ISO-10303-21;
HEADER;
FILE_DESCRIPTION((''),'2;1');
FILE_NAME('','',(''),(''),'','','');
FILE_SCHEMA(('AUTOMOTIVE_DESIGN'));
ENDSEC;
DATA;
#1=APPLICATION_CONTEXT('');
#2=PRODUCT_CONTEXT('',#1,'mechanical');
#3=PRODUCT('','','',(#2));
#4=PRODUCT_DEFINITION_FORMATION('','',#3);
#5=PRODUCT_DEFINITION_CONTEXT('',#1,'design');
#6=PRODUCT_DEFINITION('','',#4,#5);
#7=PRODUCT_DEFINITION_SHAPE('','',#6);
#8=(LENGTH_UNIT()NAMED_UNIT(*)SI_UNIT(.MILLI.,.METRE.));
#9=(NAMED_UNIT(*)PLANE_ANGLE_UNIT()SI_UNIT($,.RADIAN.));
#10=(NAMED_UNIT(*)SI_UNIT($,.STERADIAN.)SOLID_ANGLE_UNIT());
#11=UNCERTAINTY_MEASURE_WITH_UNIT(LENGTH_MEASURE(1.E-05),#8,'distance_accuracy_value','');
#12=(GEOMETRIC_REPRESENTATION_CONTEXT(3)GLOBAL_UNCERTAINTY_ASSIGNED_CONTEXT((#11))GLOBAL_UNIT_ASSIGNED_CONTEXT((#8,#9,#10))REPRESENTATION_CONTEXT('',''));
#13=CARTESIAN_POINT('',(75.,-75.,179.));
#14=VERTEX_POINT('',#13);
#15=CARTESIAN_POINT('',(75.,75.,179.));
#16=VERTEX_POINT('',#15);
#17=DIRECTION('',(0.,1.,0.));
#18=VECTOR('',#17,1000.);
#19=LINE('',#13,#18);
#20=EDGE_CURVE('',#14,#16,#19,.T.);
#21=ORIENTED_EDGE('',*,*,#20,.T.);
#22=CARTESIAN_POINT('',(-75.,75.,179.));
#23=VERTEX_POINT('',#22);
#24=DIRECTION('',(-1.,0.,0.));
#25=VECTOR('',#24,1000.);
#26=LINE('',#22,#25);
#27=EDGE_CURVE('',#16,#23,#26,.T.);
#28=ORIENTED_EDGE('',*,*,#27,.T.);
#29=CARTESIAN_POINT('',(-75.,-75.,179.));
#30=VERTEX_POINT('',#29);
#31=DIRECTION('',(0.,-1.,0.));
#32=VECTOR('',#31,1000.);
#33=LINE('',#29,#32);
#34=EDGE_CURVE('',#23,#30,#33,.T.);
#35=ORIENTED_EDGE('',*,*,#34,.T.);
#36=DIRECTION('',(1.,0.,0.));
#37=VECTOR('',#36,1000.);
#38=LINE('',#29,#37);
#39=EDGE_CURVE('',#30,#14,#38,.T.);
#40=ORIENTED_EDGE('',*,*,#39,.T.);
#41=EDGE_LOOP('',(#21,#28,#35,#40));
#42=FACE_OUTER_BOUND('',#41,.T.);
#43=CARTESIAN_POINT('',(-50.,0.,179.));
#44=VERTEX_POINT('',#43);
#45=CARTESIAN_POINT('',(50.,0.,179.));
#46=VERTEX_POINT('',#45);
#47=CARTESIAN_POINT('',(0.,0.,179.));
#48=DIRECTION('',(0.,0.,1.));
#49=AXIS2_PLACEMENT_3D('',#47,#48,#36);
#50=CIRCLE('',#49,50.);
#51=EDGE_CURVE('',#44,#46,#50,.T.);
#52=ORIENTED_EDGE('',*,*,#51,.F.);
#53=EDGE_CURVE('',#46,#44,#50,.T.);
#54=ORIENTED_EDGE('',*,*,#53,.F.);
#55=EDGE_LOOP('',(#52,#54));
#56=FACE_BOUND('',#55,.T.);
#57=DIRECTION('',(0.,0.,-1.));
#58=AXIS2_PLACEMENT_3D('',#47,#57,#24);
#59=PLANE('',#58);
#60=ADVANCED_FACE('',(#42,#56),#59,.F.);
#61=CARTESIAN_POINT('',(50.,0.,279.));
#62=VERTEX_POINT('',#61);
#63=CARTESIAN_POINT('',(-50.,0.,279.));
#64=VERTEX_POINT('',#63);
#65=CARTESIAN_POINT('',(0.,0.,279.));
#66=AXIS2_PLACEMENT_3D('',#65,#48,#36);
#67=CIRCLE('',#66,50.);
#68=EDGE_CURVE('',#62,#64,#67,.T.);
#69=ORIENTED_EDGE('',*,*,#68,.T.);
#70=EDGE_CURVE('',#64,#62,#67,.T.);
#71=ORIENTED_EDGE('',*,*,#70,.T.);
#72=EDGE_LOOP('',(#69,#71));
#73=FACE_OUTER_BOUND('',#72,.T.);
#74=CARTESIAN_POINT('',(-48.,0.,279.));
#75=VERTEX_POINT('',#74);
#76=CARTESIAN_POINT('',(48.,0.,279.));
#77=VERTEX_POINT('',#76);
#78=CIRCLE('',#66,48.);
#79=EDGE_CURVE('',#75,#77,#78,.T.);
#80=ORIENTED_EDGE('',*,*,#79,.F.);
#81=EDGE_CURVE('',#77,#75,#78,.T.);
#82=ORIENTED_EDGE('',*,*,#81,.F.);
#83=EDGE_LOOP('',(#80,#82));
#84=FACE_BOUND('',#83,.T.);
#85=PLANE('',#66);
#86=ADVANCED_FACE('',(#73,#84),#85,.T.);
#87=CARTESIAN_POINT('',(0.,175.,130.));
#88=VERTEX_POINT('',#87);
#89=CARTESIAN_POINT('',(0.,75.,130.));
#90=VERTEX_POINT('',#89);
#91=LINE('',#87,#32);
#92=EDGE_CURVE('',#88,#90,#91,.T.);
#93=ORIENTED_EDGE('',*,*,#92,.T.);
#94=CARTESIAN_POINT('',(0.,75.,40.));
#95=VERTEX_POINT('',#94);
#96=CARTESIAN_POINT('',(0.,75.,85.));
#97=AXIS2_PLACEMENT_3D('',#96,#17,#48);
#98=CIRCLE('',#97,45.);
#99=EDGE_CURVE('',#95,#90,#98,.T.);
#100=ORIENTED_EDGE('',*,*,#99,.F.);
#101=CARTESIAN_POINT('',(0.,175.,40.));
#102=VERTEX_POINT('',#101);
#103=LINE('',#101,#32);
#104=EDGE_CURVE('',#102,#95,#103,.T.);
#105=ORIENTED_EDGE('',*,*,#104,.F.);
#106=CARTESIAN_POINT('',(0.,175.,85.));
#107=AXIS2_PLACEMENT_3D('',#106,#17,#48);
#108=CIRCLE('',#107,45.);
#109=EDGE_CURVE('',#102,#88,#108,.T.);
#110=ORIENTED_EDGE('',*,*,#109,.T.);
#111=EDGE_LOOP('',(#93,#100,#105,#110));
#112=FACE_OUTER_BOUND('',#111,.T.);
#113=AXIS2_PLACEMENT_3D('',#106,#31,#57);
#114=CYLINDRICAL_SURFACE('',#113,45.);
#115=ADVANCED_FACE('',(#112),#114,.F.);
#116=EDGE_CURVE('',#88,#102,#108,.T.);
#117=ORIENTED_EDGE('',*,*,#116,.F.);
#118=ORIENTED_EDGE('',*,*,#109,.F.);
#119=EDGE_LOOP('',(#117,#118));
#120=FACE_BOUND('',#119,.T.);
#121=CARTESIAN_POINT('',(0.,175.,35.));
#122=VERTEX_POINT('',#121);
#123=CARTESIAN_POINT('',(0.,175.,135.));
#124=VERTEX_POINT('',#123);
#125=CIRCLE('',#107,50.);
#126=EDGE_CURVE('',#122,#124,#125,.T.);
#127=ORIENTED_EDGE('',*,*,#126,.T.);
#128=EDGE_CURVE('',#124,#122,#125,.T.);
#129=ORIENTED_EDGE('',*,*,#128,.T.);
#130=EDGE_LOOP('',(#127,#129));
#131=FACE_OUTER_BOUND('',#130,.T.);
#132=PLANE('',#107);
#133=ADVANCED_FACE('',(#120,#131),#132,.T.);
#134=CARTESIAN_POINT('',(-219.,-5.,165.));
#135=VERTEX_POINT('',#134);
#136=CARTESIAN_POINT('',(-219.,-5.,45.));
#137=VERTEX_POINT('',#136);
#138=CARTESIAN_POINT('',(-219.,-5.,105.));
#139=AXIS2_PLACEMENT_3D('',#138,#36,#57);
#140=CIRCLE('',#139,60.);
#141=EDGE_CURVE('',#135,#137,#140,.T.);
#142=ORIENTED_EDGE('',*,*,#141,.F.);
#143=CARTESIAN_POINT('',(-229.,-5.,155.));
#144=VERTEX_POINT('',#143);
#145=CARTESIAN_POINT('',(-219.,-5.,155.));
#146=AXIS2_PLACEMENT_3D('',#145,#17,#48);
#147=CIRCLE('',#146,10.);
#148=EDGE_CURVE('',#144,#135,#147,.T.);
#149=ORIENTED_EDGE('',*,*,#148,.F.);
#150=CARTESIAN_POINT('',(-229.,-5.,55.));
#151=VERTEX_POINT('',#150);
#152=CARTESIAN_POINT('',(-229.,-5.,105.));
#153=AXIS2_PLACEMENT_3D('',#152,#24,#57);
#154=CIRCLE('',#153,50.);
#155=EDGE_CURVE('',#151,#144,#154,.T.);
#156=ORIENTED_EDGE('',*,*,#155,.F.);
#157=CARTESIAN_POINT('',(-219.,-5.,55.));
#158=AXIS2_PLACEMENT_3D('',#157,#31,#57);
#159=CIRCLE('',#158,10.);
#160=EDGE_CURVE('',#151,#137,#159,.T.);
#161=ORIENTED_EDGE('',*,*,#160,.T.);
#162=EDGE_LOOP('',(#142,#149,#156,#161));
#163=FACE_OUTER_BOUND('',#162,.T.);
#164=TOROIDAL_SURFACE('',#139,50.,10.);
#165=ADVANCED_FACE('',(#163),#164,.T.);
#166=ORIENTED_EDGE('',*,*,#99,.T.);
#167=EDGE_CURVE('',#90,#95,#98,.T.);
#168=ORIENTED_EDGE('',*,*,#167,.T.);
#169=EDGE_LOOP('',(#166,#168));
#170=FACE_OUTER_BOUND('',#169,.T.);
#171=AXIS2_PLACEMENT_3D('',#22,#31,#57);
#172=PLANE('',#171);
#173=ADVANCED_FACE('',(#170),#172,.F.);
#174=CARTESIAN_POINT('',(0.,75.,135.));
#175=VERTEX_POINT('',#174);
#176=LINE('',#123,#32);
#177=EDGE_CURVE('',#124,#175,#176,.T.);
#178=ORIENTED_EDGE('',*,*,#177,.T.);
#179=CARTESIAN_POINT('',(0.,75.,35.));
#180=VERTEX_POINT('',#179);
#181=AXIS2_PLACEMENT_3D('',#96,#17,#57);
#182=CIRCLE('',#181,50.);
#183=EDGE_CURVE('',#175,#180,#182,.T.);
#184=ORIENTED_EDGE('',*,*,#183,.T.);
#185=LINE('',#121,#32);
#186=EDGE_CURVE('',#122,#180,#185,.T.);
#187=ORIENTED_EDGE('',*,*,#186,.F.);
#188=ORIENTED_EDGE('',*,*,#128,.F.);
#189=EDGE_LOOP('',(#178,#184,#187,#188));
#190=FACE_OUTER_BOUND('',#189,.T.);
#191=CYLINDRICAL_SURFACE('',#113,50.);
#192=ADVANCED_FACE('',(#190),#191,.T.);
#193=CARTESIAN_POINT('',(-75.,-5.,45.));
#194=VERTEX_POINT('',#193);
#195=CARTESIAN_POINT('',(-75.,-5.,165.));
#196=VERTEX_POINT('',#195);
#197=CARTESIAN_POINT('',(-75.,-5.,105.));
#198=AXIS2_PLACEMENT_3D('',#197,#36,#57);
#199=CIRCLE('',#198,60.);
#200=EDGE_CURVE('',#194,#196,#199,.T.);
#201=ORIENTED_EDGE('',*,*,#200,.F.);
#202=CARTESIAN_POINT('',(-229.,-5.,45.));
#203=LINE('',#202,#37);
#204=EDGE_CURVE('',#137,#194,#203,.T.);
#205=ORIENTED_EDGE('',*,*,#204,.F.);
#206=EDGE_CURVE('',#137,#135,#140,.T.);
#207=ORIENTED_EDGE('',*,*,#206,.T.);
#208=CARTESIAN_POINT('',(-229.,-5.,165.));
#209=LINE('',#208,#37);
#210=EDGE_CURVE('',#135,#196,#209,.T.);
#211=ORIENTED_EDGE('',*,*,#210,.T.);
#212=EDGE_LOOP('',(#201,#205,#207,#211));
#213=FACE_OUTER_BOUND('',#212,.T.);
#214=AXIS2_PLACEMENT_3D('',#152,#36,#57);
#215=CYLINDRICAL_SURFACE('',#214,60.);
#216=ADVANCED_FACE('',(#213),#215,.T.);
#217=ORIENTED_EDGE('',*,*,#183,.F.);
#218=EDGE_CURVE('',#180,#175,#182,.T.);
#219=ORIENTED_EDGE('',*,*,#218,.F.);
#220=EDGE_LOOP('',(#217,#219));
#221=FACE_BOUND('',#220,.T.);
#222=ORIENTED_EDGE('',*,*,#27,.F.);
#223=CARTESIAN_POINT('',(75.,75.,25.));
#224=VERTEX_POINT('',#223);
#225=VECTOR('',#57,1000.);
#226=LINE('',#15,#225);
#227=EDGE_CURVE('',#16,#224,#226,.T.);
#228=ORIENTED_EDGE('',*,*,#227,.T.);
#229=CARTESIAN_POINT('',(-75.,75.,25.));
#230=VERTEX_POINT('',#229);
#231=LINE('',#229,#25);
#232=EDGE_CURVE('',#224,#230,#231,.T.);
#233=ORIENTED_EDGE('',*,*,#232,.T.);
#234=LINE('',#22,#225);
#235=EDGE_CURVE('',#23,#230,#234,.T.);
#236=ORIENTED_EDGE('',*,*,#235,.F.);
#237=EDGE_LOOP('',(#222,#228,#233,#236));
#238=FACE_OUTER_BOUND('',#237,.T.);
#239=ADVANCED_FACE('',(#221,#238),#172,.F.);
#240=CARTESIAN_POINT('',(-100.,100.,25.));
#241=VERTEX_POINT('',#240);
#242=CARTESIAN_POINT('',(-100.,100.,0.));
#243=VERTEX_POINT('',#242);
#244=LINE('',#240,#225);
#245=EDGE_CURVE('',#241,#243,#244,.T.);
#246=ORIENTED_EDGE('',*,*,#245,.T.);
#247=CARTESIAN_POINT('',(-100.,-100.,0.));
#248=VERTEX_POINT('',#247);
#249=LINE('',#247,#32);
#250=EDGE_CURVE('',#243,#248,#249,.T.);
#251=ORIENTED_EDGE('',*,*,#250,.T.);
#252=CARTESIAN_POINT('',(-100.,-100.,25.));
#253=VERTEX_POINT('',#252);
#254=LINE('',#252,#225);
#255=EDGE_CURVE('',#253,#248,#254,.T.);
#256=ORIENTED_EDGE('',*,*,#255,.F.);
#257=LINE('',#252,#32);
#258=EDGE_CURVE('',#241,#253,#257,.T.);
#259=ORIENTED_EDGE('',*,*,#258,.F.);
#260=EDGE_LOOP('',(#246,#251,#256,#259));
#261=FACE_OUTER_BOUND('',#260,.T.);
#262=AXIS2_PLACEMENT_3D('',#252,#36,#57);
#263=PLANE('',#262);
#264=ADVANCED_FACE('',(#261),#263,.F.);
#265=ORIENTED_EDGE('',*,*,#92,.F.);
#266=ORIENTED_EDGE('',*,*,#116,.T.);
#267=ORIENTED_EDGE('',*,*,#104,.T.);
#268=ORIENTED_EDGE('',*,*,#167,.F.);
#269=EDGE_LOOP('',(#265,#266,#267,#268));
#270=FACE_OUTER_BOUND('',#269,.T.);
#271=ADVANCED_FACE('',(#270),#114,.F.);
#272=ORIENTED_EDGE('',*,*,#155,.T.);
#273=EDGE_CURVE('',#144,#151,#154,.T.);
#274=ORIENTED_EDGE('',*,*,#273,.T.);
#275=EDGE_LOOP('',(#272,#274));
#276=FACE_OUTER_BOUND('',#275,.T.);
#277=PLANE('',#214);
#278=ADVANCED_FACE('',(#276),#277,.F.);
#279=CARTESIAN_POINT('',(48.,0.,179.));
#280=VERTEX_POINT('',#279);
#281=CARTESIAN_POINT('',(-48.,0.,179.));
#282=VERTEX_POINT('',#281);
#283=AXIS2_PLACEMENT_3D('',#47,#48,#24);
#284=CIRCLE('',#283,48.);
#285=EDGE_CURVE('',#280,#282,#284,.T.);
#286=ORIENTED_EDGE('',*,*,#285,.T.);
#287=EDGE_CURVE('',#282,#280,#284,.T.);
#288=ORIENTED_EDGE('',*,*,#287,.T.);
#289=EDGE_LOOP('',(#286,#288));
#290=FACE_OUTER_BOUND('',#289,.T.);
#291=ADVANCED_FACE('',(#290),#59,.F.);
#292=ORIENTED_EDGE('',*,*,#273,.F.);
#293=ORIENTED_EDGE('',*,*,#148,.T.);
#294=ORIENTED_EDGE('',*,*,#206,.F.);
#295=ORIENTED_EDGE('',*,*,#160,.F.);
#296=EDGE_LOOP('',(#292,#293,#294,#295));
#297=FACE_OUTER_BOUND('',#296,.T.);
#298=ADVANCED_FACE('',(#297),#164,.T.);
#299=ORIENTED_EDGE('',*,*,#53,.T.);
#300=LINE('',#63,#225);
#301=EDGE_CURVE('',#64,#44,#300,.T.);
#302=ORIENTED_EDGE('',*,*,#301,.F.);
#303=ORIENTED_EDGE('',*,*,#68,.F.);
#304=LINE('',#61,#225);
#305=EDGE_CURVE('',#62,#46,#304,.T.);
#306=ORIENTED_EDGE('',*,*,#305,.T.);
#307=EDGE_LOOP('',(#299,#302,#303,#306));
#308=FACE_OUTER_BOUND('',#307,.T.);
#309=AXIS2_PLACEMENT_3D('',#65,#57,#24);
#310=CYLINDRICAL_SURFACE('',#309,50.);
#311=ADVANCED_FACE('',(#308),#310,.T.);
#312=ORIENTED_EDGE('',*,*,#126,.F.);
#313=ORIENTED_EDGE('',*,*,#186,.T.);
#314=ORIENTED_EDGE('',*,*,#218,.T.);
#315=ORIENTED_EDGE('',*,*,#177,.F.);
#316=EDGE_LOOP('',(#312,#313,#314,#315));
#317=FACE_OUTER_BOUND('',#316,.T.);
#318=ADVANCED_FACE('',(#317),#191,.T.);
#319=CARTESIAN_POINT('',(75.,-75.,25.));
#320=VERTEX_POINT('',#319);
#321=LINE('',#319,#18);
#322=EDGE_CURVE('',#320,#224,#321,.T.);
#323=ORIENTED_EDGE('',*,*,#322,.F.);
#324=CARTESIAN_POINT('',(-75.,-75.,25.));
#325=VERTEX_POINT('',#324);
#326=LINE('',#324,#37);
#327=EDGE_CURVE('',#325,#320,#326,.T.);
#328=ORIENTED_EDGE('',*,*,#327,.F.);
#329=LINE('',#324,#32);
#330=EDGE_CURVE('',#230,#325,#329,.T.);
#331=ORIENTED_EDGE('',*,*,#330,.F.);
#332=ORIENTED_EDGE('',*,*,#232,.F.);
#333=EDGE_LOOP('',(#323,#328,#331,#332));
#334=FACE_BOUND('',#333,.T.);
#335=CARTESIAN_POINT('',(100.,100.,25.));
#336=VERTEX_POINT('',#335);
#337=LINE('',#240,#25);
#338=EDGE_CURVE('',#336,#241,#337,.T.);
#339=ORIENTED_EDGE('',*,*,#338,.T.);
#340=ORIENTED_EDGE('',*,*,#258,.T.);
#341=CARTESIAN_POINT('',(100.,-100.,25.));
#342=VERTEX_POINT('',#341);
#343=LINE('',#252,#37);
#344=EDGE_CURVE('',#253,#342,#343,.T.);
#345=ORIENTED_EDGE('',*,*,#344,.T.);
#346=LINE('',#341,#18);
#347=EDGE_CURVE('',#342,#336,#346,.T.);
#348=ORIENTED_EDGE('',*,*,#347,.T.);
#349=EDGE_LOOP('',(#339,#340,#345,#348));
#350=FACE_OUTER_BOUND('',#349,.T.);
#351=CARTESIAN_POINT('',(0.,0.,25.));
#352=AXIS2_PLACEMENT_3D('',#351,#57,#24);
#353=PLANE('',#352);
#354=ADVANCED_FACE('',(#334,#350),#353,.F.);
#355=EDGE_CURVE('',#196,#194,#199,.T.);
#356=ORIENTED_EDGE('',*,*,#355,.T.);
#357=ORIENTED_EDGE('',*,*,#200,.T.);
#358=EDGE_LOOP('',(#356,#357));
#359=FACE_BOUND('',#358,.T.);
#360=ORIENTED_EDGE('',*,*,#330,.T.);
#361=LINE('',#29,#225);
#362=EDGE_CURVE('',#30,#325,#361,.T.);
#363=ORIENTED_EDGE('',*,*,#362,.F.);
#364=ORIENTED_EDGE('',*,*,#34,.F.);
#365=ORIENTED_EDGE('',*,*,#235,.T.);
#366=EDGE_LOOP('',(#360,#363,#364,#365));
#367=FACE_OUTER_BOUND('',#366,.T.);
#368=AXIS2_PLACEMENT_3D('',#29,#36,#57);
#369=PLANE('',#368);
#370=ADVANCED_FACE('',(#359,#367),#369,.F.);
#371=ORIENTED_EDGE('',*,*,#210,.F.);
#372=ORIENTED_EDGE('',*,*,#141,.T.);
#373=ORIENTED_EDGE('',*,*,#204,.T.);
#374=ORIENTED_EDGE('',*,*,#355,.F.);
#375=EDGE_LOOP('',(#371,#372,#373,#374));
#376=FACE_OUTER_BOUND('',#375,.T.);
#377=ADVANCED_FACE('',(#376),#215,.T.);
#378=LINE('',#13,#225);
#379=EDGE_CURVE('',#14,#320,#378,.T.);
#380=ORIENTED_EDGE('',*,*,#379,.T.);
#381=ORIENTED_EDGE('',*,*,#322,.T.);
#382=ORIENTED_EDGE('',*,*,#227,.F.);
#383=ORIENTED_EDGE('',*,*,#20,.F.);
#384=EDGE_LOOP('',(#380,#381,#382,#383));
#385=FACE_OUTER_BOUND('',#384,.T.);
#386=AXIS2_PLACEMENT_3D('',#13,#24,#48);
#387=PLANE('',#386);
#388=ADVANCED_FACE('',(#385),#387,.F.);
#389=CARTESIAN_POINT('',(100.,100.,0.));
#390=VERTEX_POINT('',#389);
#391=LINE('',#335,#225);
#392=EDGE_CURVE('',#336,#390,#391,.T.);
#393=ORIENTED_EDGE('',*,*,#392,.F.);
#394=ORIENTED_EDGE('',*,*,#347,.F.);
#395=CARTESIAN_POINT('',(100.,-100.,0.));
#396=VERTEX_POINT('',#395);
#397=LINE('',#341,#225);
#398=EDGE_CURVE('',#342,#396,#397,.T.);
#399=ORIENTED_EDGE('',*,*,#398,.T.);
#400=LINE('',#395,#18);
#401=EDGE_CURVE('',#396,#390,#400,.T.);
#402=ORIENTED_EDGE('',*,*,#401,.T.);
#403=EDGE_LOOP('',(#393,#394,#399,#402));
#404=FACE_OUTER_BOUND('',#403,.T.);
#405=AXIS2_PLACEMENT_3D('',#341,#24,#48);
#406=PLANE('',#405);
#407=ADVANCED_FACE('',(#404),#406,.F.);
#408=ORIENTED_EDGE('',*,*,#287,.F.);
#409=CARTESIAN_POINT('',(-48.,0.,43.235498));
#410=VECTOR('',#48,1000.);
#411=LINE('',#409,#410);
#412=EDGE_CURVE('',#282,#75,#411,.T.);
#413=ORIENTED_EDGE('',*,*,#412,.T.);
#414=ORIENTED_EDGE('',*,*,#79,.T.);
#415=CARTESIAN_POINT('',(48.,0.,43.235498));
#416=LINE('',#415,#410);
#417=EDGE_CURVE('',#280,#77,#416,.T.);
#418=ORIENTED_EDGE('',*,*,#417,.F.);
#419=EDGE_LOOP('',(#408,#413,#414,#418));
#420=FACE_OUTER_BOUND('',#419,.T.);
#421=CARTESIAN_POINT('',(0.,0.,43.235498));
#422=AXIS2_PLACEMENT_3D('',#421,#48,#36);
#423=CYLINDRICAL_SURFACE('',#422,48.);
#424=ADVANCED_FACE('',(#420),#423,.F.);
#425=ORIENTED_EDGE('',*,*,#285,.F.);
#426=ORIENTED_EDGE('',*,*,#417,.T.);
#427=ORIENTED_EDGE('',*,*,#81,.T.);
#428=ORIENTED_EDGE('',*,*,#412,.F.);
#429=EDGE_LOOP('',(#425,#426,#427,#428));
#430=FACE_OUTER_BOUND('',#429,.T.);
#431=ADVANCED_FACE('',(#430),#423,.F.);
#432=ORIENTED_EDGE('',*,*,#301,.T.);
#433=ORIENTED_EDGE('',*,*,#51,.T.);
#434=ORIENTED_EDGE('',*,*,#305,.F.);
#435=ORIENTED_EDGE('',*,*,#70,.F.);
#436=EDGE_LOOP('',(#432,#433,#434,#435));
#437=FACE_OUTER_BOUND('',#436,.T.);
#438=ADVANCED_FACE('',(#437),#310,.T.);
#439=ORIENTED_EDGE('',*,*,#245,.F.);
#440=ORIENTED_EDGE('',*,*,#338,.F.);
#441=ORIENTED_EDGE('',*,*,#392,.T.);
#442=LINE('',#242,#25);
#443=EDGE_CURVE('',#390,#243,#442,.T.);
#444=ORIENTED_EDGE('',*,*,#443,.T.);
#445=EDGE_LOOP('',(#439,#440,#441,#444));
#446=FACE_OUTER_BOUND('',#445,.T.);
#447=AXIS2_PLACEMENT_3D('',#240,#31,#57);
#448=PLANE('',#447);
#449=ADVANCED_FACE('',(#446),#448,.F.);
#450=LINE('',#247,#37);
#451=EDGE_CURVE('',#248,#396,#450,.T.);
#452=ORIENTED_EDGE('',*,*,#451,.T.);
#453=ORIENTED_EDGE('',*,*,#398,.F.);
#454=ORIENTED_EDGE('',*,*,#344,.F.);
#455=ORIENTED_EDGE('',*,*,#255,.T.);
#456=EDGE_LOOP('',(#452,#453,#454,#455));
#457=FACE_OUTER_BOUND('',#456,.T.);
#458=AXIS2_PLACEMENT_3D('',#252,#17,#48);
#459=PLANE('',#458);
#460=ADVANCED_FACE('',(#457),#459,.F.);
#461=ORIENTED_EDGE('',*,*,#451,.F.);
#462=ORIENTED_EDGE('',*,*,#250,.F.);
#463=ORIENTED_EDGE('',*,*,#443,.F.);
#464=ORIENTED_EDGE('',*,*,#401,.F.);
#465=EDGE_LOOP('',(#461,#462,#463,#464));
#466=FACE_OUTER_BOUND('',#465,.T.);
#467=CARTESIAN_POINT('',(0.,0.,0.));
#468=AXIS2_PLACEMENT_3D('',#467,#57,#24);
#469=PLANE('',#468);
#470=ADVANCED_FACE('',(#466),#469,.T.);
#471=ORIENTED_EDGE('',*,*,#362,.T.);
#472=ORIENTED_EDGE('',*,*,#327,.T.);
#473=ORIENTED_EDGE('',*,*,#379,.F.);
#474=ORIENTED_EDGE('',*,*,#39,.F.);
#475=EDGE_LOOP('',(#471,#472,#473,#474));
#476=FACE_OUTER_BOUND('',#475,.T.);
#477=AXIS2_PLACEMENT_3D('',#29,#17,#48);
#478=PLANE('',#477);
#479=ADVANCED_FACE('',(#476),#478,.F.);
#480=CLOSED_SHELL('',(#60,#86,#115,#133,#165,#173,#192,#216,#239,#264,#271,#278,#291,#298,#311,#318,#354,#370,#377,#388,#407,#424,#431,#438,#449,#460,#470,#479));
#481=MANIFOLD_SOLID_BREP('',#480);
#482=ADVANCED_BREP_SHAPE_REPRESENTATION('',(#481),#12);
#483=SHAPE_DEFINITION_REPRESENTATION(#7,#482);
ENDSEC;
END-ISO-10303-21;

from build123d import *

# Parameters (mm, degrees)
SKETCH_1_W          = 200
SKETCH_1_H          = 200
EXTRUDE_1_DEPTH     = 25
SKETCH_2_W          = 150
SKETCH_2_H          = 150
EXTRUDE_2_DEPTH     = 154
SKETCH_3_R          = 60
EXTRUDE_3_DEPTH     = 154
FILLET_1_R          = 10
SKETCH_4_R          = 50
EXTRUDE_4_DEPTH     = 100
SKETCH_5_R          = 50
SKETCH_5_R_2        = 45
EXTRUDE_5_DEPTH     = 100
SKETCH_6_R          = 48
CUT_EXTRUDE_1_DEPTH = 100


with BuildPart() as part:
    # 草图1 → 凸台-拉伸1 (new body)
    with BuildSketch(Plane.XY):
        Rectangle(SKETCH_1_W, SKETCH_1_H)
    extrude(amount=EXTRUDE_1_DEPTH)

    # 草图2 → 凸台-拉伸2 (add)
    with BuildSketch(Plane.XY.offset(25)):
        Rectangle(SKETCH_2_W, SKETCH_2_H)
    extrude(amount=EXTRUDE_2_DEPTH)

    # 草图3 → 凸台-拉伸3 (add)
    with BuildSketch(Plane(origin=(-75, 0, 0), x_dir=(0, 0, -1), z_dir=(1, 0, 0))):
        with Locations((-105, -5)):
            Circle(SKETCH_3_R)
    extrude(amount=-EXTRUDE_3_DEPTH)

    # 圆角1
    fillet_1_edges = [part.edges().sort_by_distance(p)[0] for p in [
        (-229, -5, 165),
    ]]
    fillet(fillet_1_edges, radius=FILLET_1_R)

    # 草图4 → 凸台-拉伸4 (add)
    with BuildSketch(Plane.XY.offset(179)):
        Circle(SKETCH_4_R)
    extrude(amount=EXTRUDE_4_DEPTH)

    # 草图5 → 凸台-拉伸5 (add)
    with BuildSketch(Plane(origin=(0, 75, 0), x_dir=(1, 0, 0), z_dir=(0, 1, 0))):
        with Locations(Location((0, -85, 0), (0, 0, 90))):
            Circle(SKETCH_5_R)
        with Locations(Location((0, -85, 0), (0, 0, 270))):
            Circle(SKETCH_5_R_2, mode=Mode.SUBTRACT)
    extrude(amount=EXTRUDE_5_DEPTH)

    # 草图6 → 切除-拉伸1 (cut)
    with BuildSketch(Plane.XY.offset(279)):
        Circle(SKETCH_6_R)
    extrude(amount=-CUT_EXTRUDE_1_DEPTH, mode=Mode.SUBTRACT)


solid = part.part
